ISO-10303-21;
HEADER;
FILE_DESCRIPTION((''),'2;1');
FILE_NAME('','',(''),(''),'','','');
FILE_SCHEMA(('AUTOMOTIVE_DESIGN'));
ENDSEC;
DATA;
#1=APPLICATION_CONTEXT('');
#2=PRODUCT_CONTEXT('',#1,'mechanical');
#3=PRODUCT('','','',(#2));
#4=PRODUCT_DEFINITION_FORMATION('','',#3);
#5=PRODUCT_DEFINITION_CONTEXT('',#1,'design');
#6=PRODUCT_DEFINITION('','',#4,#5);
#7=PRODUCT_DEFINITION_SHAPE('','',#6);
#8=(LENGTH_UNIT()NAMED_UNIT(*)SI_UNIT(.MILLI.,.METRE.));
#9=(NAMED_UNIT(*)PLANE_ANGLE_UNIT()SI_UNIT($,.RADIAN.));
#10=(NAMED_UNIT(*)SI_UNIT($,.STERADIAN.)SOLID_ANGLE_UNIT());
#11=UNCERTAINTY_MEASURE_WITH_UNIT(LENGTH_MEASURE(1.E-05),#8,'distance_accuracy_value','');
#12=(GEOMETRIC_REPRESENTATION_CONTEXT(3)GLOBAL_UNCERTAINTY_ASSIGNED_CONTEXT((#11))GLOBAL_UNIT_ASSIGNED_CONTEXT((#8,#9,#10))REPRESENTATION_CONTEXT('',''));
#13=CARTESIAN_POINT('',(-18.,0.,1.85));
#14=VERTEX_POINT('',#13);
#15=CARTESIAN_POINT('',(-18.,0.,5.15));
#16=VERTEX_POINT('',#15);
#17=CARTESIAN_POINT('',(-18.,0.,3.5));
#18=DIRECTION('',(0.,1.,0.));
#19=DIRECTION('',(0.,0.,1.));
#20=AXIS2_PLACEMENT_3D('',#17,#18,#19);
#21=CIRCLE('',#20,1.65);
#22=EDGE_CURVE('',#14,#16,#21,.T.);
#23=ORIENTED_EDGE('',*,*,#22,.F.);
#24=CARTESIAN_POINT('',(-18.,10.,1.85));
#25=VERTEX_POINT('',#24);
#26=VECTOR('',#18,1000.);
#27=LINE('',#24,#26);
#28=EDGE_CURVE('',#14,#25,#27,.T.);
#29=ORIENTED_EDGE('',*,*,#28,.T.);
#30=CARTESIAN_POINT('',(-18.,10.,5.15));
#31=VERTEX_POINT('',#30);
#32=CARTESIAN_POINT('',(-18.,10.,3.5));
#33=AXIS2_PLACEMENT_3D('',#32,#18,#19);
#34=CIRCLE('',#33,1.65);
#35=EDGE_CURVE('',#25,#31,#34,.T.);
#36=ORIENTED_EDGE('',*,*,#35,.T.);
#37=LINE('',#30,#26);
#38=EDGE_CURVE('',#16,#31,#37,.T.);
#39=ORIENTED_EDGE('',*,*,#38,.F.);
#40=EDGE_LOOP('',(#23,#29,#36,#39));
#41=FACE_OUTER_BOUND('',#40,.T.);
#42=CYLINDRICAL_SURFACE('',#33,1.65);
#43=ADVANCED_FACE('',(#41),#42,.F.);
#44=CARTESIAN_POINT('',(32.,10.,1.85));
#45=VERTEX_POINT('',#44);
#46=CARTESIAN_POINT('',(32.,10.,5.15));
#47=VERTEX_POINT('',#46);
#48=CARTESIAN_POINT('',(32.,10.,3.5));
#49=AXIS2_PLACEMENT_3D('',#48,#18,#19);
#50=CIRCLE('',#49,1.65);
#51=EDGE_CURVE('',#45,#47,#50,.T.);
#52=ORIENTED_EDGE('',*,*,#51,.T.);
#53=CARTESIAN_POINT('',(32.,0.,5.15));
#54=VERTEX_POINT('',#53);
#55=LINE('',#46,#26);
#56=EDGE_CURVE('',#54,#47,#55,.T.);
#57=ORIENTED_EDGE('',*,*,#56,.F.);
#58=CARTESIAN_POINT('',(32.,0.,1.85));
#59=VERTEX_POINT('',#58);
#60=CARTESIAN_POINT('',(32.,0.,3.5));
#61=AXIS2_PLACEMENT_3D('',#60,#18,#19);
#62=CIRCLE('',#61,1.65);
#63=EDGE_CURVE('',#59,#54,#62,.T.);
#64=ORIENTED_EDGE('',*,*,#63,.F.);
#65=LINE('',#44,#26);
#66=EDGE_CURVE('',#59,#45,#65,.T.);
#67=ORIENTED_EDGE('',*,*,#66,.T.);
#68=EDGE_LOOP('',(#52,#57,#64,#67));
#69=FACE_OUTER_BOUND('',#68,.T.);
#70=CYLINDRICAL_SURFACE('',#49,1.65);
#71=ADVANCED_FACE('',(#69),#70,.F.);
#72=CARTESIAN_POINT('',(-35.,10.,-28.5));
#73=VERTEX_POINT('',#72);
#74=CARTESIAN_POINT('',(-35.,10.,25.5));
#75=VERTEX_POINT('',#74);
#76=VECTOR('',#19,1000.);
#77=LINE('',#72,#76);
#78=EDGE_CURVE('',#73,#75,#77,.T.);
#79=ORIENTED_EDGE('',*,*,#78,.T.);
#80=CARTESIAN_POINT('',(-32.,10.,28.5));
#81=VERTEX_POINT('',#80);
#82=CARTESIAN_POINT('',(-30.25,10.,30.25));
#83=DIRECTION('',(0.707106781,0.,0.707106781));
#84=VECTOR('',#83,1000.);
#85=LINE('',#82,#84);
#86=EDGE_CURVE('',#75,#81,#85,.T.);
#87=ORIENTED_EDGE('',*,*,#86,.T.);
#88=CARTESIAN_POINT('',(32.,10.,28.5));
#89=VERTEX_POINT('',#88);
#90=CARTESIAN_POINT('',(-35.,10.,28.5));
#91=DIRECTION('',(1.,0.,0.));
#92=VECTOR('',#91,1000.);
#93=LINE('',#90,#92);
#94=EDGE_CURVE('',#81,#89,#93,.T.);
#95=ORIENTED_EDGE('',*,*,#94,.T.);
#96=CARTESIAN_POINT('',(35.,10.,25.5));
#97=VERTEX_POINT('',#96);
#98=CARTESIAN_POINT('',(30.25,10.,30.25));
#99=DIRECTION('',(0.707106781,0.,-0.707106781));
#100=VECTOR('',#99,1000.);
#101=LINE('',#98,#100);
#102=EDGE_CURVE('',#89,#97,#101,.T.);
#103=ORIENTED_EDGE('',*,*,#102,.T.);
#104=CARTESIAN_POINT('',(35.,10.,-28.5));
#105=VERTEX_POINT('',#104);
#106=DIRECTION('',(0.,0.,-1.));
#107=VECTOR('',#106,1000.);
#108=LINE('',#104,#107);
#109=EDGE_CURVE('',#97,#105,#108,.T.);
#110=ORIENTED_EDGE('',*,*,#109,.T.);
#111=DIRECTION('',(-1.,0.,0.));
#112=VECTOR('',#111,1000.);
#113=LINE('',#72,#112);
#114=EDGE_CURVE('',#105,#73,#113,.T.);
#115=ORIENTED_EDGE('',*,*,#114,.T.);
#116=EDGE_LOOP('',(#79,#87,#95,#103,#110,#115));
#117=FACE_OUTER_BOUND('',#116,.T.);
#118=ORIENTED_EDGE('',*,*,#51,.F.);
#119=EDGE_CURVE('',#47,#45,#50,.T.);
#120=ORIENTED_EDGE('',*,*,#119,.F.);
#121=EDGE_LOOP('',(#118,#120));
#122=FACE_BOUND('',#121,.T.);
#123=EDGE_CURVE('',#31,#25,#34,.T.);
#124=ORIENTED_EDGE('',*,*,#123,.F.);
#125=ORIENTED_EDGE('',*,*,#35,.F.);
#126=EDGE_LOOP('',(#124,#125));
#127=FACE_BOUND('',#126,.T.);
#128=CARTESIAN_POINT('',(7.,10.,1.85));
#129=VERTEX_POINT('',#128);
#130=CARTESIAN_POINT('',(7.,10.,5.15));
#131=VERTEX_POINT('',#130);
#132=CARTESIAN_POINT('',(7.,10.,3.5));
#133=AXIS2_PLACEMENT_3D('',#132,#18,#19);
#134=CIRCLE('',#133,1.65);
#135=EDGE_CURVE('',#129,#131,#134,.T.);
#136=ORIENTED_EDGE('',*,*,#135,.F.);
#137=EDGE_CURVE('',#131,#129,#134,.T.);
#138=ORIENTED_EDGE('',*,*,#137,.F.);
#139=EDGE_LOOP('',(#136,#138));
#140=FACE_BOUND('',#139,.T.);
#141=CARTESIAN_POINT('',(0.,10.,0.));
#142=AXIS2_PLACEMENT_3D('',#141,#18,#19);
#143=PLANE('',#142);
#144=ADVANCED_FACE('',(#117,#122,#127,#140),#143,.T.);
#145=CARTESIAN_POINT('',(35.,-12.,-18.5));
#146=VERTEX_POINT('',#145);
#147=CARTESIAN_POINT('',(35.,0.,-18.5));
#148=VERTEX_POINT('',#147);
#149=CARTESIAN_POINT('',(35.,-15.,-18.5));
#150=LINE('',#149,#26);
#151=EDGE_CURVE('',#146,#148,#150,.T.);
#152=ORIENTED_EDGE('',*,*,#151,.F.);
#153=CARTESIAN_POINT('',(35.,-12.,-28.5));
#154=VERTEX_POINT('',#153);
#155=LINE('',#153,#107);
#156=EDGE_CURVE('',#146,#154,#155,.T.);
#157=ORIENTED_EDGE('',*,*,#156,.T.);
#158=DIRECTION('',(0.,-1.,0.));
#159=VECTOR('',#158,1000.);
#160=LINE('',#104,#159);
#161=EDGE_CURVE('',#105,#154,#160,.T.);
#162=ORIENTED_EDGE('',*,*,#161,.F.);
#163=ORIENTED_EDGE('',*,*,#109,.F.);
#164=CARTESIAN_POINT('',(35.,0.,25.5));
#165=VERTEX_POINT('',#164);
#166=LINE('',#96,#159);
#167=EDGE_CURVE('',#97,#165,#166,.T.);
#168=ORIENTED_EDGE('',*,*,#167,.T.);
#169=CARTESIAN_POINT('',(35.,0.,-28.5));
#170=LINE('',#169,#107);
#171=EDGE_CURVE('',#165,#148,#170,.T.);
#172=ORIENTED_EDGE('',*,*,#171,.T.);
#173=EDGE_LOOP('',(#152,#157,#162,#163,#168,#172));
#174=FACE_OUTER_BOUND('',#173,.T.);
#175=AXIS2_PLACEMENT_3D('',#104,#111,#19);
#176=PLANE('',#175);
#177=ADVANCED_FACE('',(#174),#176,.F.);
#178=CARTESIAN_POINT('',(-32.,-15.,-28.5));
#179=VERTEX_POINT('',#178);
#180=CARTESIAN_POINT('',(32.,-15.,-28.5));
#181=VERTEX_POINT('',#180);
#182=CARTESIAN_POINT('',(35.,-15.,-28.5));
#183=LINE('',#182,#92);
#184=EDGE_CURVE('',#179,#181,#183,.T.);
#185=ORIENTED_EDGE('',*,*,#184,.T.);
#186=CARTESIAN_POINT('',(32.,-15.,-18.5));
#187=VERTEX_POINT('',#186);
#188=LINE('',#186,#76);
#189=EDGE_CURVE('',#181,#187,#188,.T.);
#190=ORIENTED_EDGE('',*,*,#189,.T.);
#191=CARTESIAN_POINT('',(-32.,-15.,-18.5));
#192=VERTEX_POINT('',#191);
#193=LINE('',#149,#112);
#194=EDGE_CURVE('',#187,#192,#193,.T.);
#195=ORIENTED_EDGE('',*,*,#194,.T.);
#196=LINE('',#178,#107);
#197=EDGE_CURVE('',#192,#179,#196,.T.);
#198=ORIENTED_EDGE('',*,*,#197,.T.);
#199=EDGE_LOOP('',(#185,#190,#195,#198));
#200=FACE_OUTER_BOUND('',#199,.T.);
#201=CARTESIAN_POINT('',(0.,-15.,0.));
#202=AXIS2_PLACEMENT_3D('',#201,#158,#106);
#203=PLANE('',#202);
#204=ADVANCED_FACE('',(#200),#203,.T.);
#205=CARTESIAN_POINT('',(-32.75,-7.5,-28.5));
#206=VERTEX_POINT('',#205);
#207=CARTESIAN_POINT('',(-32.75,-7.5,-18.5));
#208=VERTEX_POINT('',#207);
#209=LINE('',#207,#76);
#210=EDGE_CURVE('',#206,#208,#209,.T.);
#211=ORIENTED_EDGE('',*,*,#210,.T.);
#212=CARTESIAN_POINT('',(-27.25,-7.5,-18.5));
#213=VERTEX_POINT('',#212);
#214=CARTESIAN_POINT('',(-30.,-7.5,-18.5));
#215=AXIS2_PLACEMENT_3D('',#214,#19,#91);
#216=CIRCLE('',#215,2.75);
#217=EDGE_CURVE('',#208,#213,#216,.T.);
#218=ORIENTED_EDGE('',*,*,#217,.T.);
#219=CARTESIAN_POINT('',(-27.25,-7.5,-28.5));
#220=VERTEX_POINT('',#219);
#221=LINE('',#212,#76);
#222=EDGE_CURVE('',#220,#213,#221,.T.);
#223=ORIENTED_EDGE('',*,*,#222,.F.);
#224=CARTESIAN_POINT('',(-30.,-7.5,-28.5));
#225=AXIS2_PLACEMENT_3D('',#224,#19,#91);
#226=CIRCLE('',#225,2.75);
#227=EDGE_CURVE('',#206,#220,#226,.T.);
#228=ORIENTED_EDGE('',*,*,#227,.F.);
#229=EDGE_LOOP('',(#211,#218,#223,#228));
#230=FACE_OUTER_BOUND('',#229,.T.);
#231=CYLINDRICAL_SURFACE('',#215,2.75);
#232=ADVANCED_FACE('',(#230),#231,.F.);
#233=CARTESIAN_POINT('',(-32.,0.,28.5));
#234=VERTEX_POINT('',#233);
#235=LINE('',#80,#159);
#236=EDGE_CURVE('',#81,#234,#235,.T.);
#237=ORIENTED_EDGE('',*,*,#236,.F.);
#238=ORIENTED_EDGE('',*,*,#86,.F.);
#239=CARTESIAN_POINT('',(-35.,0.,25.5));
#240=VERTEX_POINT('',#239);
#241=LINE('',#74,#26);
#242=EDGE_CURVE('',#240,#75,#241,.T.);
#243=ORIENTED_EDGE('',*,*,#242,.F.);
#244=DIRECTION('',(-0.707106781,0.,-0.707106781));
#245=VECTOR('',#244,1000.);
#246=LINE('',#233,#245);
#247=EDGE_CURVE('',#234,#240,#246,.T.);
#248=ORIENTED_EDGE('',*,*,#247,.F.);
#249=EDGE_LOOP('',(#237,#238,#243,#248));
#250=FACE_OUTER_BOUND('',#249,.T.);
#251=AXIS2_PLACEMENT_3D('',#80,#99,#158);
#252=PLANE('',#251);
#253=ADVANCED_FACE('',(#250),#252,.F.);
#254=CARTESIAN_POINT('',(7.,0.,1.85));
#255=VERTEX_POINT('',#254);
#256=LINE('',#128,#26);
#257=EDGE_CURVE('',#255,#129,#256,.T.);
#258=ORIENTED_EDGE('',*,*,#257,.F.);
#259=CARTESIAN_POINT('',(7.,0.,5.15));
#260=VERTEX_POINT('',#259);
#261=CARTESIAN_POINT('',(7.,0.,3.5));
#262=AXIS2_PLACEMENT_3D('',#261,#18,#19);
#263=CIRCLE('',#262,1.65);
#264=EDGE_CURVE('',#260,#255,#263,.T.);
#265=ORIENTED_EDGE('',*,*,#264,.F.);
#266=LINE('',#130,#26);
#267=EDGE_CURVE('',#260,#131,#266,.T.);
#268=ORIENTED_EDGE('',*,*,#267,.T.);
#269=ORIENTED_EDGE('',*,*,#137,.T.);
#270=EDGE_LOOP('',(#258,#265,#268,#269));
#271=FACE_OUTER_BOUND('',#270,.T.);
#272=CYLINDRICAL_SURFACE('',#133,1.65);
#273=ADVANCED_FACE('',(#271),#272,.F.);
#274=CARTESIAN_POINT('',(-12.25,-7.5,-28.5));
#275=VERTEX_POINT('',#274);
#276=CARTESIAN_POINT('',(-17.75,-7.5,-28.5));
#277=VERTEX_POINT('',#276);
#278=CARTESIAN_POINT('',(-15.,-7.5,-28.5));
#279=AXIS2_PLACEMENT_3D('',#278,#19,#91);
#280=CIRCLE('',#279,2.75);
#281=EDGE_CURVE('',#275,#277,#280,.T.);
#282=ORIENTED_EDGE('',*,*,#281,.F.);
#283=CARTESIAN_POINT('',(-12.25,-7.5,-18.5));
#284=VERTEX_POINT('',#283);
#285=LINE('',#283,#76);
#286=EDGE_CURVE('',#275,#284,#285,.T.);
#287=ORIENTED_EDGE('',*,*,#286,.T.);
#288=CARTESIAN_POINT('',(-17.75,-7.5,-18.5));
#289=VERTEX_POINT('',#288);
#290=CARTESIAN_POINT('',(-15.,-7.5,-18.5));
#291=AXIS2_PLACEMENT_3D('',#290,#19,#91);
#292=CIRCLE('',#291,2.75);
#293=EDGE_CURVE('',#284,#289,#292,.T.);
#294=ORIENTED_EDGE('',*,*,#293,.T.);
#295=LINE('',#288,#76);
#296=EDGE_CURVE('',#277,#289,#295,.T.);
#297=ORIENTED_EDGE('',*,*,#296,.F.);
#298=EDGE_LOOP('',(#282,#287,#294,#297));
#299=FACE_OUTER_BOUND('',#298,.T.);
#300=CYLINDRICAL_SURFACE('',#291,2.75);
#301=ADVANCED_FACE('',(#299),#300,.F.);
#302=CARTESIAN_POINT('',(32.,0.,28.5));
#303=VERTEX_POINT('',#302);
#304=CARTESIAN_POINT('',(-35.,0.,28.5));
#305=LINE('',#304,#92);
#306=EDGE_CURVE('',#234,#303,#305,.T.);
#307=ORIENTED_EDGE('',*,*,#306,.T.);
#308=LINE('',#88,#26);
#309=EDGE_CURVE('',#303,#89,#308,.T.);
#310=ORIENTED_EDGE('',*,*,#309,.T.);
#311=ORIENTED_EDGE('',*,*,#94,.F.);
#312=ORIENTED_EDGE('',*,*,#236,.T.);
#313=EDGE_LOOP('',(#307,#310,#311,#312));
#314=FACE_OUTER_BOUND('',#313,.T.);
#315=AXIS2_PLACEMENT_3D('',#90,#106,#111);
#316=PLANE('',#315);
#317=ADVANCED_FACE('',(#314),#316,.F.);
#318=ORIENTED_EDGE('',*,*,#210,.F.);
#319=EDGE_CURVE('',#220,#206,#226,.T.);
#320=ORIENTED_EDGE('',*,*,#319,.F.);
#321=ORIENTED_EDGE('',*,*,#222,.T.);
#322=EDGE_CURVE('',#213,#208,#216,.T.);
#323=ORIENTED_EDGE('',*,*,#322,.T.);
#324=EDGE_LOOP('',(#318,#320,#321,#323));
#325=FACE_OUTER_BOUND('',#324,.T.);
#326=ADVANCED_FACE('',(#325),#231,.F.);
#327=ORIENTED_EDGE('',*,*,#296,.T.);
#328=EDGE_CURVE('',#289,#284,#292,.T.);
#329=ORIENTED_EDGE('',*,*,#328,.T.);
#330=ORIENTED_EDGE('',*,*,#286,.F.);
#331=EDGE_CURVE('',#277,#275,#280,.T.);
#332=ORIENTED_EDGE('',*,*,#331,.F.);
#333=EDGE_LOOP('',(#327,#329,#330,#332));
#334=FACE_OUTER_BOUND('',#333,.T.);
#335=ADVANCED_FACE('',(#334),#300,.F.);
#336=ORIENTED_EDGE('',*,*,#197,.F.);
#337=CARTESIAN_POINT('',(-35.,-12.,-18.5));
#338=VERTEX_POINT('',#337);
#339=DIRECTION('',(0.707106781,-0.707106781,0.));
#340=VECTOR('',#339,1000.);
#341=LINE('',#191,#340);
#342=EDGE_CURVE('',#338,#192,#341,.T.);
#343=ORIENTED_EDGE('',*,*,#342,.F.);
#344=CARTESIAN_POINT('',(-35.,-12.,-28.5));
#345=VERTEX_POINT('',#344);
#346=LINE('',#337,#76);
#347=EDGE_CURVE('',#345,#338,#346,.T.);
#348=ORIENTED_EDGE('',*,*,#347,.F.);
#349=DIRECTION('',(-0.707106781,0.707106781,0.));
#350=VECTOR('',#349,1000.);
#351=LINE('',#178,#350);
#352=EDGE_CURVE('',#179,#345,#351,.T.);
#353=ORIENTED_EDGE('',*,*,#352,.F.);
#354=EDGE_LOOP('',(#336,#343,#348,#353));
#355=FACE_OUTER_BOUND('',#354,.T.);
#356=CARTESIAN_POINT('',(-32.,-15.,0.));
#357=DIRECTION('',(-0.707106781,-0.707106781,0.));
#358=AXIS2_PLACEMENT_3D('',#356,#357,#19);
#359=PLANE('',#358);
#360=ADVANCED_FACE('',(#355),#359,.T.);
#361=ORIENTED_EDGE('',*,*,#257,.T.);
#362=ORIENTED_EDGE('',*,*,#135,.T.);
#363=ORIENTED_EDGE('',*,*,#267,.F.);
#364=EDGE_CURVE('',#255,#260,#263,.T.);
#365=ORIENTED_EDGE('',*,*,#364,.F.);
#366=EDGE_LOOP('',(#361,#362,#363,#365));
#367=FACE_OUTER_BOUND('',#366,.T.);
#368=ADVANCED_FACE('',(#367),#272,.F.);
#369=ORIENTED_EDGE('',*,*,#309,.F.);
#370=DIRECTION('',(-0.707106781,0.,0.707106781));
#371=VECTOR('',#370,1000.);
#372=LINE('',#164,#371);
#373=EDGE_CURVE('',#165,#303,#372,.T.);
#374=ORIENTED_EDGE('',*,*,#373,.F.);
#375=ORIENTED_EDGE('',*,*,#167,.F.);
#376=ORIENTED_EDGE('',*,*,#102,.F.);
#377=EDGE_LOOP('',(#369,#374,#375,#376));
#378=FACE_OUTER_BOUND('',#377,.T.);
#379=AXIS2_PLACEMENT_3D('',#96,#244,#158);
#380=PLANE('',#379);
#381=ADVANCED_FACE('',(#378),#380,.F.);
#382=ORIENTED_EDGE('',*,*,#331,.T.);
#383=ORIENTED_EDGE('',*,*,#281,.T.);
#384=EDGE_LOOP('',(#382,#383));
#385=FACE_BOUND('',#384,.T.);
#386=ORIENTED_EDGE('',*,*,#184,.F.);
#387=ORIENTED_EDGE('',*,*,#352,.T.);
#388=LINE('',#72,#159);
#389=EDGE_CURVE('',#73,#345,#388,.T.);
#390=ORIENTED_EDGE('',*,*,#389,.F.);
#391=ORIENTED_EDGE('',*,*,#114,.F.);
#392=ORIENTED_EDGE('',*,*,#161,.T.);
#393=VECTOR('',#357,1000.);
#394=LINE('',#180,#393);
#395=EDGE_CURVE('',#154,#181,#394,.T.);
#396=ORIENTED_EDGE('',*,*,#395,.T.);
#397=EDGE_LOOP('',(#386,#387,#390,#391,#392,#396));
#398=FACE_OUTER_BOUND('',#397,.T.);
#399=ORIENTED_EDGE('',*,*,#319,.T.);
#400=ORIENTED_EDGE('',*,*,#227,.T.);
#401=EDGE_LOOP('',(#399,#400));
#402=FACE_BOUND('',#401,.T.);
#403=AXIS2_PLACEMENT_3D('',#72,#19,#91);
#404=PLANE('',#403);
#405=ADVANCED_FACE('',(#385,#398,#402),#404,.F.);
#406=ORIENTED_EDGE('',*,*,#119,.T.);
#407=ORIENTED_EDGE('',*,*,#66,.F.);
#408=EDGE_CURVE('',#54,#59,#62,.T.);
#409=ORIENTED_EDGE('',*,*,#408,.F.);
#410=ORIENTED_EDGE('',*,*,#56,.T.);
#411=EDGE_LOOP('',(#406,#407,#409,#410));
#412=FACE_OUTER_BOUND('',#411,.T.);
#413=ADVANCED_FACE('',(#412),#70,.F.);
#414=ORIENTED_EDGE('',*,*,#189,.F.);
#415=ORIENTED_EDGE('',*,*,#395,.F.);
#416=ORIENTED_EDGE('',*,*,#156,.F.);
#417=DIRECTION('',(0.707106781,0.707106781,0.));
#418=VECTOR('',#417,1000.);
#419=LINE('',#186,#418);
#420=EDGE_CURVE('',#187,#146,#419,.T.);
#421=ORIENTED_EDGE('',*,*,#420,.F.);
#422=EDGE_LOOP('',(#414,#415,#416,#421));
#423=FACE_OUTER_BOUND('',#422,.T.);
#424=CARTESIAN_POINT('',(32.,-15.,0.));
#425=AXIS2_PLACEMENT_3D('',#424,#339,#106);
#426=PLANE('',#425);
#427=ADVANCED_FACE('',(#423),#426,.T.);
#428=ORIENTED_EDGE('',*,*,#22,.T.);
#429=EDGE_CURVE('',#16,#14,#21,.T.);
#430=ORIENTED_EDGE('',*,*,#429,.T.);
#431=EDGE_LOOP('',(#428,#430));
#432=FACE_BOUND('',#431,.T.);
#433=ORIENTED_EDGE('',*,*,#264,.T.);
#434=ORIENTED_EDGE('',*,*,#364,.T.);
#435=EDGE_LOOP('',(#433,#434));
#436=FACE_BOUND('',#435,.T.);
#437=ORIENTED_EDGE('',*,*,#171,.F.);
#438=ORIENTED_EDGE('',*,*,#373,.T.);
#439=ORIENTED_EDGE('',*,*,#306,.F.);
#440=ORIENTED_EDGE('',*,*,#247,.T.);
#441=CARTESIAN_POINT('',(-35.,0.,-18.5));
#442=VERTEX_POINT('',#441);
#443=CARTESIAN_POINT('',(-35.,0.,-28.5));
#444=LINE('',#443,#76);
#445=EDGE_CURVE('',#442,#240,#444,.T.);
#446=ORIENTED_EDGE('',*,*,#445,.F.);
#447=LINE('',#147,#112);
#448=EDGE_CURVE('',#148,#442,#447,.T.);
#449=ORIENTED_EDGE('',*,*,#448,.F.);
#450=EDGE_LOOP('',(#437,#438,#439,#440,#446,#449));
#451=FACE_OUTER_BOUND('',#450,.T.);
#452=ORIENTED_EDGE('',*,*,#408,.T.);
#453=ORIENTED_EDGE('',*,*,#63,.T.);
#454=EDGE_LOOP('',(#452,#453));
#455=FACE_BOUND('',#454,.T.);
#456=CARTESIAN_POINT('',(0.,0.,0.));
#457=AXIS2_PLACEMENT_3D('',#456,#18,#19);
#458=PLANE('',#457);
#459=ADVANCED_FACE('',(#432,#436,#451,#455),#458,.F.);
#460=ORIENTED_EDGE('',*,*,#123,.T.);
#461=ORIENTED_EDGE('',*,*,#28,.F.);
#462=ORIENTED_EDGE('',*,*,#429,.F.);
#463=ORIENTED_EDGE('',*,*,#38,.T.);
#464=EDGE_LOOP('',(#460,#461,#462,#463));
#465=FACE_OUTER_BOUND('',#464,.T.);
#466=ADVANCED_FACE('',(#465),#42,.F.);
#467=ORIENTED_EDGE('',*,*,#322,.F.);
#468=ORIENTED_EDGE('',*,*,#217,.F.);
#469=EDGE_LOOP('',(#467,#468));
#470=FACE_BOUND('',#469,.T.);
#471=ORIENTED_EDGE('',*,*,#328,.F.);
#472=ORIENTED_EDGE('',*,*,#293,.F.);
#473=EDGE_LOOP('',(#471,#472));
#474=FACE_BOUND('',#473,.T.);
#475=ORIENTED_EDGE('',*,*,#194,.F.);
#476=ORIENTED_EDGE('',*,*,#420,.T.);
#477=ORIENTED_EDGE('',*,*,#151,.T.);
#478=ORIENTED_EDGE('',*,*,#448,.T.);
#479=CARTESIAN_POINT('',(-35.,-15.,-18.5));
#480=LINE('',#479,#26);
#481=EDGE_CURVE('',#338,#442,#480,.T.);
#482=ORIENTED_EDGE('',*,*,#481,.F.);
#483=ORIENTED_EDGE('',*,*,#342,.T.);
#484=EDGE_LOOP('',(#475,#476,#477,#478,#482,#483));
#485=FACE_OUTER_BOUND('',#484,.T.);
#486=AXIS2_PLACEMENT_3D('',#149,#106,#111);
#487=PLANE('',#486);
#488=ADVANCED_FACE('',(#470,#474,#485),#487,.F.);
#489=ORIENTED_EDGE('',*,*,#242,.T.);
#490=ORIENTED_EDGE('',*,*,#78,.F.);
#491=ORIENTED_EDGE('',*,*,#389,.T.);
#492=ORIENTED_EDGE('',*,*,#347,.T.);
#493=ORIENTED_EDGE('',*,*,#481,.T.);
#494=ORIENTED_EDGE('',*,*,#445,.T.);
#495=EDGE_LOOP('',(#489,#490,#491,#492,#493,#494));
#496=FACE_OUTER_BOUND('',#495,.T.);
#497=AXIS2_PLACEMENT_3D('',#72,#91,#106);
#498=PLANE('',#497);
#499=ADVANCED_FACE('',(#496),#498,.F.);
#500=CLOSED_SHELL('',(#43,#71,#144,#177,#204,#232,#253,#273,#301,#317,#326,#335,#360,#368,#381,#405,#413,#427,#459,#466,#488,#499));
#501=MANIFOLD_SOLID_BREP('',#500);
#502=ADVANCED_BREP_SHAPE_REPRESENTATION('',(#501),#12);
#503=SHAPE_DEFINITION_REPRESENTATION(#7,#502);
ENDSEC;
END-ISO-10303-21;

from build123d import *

# Parameters (mm, degrees)
SKETCH_1_W                  = 70
SKETCH_1_H                  = 57
EXTRUDE_1_DEPTH             = 10
SKETCH_2_W                  = 70
SKETCH_2_H                  = 10
EXTRUDE_2_DEPTH             = 15
CHAMFER_1_SIZE              = 3
HOLE_WIZARD_M4_1_D          = 3.3
HOLE_WIZARD_M4_1_DEPTH      = 10.1
HOLE_WIZARD_M4_1_TIP        = 0.991420021
HOLE_WIZARD_5_5_5_5_1_D     = 5.5
HOLE_WIZARD_5_5_5_5_1_DEPTH = 10.1
HOLE_WIZARD_5_5_5_5_1_TIP   = 1.652366702


with BuildPart() as part:
    # 草图1 → 凸台-拉伸1 (new body)
    with BuildSketch(Plane(origin=(0, 0, 0), x_dir=(1, 0, 0), z_dir=(0, 1, 0))):
        Rectangle(SKETCH_1_W, SKETCH_1_H)
    extrude(amount=EXTRUDE_1_DEPTH)

    # 草图2 → 凸台-拉伸2 (add)
    with BuildSketch(Plane.XZ):
        with Locations((0, -23.5)):
            Rectangle(SKETCH_2_W, SKETCH_2_H)
    extrude(amount=EXTRUDE_2_DEPTH)

    # 倒角1
    chamfer_1_edges = [part.edges().sort_by_distance(p)[0] for p in [
        (35, -15, -23.5),
        (-35, -15, -23.5),
        (35, 5, 28.5),
        (-35, 5, 28.5),
    ]]
    chamfer(chamfer_1_edges, length=CHAMFER_1_SIZE)

    # M4 螺纹孔1
    with Locations(Plane(origin=(0, 10, 0), x_dir=(1, 0, 0), z_dir=(0, 1, 0))):
        with Locations((32, -3.5), (-18, -3.5), (7, -3.5)):
            Hole(HOLE_WIZARD_M4_1_D / 2, depth=HOLE_WIZARD_M4_1_DEPTH)
            with Locations((0, 0, -(HOLE_WIZARD_M4_1_DEPTH + HOLE_WIZARD_M4_1_TIP / 2))):  # 118° drill point
                Cone(0, HOLE_WIZARD_M4_1_D / 2, HOLE_WIZARD_M4_1_TIP, mode=Mode.SUBTRACT)

    # Ø5.5 (5.5) 直径孔1
    with Locations(Plane.XY.offset(-18.5)):
        with Locations((-15, -7.5), (-30, -7.5)):
            Hole(HOLE_WIZARD_5_5_5_5_1_D / 2, depth=HOLE_WIZARD_5_5_5_5_1_DEPTH)
            with Locations((0, 0, -(HOLE_WIZARD_5_5_5_5_1_DEPTH + HOLE_WIZARD_5_5_5_5_1_TIP / 2))):  # 118° drill point
                Cone(0, HOLE_WIZARD_5_5_5_5_1_D / 2, HOLE_WIZARD_5_5_5_5_1_TIP, mode=Mode.SUBTRACT)


solid = part.part
